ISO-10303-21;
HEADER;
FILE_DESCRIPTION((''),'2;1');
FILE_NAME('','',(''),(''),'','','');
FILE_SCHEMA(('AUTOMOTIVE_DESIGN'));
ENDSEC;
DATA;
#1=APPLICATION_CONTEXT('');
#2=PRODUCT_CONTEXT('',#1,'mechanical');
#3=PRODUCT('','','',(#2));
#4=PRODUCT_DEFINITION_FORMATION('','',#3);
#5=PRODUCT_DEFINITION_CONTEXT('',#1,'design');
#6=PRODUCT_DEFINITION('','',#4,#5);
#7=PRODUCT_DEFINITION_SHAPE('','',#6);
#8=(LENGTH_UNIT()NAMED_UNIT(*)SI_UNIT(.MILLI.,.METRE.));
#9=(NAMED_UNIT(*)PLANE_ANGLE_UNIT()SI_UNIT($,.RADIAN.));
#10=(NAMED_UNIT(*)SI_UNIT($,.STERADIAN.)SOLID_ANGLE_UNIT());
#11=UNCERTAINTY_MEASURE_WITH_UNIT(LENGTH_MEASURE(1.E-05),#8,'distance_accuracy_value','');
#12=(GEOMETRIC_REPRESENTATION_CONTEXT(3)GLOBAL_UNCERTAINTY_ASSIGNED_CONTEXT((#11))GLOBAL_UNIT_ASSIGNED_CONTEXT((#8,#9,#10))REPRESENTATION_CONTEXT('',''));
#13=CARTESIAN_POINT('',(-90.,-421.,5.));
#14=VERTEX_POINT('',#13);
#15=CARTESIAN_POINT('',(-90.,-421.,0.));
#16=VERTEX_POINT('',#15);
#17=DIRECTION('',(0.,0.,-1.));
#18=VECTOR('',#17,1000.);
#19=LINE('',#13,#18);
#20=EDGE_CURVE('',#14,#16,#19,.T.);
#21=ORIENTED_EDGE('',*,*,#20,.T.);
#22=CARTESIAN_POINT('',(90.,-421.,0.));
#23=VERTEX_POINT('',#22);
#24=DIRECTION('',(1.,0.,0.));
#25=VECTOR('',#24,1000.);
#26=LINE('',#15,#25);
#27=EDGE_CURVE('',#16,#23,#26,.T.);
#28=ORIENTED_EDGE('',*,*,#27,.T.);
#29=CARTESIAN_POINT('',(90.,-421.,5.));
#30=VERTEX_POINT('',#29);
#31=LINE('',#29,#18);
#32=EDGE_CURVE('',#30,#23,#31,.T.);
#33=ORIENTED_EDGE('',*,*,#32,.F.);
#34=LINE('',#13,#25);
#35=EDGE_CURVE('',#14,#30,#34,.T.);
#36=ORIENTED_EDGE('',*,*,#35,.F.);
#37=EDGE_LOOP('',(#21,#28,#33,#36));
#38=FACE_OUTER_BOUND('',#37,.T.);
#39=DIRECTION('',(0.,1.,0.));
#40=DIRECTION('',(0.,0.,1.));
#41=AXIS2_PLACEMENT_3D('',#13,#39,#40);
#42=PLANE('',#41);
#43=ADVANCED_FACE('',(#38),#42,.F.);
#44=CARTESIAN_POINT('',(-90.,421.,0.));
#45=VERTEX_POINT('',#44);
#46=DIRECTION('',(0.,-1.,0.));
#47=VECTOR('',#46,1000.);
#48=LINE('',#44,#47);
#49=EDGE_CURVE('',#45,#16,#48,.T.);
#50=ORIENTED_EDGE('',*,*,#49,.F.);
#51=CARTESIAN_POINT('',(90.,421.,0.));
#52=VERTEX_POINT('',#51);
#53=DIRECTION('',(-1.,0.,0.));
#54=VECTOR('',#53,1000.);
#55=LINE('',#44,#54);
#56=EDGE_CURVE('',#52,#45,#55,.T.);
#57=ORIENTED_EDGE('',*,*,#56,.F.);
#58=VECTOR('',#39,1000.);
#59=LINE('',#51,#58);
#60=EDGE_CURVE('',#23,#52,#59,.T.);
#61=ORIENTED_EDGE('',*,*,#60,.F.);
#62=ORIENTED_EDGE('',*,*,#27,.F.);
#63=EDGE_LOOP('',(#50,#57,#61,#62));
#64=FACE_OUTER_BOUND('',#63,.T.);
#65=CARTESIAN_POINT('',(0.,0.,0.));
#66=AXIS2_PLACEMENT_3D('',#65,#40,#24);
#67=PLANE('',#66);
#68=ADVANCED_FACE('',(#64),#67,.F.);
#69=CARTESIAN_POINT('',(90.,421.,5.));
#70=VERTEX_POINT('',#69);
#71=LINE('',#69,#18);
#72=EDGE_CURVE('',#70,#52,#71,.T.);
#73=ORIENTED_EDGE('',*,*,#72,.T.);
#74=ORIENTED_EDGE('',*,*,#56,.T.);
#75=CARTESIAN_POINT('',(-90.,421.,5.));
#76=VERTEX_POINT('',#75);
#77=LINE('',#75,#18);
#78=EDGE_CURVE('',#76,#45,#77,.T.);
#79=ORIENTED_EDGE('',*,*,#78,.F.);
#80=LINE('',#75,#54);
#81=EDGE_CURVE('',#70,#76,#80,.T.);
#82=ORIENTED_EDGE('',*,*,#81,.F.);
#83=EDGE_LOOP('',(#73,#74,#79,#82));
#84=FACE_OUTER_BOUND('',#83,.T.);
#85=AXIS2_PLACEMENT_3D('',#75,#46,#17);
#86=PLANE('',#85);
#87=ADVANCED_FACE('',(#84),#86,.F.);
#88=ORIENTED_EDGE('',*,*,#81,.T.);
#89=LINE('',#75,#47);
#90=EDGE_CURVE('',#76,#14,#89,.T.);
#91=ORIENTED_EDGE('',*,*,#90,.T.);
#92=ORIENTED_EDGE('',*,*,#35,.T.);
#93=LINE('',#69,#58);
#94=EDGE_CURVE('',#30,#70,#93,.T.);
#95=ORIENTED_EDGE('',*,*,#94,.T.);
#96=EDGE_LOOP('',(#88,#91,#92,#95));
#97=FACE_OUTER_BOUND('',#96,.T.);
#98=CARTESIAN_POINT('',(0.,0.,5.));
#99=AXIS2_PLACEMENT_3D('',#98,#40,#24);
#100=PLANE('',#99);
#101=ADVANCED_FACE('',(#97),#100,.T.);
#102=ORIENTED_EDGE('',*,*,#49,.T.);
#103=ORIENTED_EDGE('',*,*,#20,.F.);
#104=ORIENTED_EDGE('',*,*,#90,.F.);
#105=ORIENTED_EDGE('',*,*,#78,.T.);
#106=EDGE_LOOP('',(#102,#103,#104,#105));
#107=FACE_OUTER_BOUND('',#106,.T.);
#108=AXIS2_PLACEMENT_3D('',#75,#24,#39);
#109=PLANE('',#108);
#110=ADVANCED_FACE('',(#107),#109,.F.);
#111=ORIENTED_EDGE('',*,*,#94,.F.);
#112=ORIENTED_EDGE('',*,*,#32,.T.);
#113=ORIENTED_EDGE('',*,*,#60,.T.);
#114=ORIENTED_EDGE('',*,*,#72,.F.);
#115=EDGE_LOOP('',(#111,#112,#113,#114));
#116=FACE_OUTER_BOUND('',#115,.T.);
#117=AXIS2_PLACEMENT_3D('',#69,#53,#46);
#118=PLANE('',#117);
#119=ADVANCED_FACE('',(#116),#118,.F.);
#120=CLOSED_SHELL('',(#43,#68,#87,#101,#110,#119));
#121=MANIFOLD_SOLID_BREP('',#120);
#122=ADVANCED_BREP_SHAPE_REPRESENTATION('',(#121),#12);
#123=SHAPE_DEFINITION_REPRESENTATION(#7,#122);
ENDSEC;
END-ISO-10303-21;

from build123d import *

# Parameters (mm, degrees)
SKETCH_1_W      = 180
SKETCH_1_H      = 842
EXTRUDE_1_DEPTH = 5


with BuildPart() as part:
    # 草图1 → 凸台-拉伸1 (new body)
    with BuildSketch(Plane.XY):
        Rectangle(SKETCH_1_W, SKETCH_1_H)
    extrude(amount=EXTRUDE_1_DEPTH)


solid = part.part
